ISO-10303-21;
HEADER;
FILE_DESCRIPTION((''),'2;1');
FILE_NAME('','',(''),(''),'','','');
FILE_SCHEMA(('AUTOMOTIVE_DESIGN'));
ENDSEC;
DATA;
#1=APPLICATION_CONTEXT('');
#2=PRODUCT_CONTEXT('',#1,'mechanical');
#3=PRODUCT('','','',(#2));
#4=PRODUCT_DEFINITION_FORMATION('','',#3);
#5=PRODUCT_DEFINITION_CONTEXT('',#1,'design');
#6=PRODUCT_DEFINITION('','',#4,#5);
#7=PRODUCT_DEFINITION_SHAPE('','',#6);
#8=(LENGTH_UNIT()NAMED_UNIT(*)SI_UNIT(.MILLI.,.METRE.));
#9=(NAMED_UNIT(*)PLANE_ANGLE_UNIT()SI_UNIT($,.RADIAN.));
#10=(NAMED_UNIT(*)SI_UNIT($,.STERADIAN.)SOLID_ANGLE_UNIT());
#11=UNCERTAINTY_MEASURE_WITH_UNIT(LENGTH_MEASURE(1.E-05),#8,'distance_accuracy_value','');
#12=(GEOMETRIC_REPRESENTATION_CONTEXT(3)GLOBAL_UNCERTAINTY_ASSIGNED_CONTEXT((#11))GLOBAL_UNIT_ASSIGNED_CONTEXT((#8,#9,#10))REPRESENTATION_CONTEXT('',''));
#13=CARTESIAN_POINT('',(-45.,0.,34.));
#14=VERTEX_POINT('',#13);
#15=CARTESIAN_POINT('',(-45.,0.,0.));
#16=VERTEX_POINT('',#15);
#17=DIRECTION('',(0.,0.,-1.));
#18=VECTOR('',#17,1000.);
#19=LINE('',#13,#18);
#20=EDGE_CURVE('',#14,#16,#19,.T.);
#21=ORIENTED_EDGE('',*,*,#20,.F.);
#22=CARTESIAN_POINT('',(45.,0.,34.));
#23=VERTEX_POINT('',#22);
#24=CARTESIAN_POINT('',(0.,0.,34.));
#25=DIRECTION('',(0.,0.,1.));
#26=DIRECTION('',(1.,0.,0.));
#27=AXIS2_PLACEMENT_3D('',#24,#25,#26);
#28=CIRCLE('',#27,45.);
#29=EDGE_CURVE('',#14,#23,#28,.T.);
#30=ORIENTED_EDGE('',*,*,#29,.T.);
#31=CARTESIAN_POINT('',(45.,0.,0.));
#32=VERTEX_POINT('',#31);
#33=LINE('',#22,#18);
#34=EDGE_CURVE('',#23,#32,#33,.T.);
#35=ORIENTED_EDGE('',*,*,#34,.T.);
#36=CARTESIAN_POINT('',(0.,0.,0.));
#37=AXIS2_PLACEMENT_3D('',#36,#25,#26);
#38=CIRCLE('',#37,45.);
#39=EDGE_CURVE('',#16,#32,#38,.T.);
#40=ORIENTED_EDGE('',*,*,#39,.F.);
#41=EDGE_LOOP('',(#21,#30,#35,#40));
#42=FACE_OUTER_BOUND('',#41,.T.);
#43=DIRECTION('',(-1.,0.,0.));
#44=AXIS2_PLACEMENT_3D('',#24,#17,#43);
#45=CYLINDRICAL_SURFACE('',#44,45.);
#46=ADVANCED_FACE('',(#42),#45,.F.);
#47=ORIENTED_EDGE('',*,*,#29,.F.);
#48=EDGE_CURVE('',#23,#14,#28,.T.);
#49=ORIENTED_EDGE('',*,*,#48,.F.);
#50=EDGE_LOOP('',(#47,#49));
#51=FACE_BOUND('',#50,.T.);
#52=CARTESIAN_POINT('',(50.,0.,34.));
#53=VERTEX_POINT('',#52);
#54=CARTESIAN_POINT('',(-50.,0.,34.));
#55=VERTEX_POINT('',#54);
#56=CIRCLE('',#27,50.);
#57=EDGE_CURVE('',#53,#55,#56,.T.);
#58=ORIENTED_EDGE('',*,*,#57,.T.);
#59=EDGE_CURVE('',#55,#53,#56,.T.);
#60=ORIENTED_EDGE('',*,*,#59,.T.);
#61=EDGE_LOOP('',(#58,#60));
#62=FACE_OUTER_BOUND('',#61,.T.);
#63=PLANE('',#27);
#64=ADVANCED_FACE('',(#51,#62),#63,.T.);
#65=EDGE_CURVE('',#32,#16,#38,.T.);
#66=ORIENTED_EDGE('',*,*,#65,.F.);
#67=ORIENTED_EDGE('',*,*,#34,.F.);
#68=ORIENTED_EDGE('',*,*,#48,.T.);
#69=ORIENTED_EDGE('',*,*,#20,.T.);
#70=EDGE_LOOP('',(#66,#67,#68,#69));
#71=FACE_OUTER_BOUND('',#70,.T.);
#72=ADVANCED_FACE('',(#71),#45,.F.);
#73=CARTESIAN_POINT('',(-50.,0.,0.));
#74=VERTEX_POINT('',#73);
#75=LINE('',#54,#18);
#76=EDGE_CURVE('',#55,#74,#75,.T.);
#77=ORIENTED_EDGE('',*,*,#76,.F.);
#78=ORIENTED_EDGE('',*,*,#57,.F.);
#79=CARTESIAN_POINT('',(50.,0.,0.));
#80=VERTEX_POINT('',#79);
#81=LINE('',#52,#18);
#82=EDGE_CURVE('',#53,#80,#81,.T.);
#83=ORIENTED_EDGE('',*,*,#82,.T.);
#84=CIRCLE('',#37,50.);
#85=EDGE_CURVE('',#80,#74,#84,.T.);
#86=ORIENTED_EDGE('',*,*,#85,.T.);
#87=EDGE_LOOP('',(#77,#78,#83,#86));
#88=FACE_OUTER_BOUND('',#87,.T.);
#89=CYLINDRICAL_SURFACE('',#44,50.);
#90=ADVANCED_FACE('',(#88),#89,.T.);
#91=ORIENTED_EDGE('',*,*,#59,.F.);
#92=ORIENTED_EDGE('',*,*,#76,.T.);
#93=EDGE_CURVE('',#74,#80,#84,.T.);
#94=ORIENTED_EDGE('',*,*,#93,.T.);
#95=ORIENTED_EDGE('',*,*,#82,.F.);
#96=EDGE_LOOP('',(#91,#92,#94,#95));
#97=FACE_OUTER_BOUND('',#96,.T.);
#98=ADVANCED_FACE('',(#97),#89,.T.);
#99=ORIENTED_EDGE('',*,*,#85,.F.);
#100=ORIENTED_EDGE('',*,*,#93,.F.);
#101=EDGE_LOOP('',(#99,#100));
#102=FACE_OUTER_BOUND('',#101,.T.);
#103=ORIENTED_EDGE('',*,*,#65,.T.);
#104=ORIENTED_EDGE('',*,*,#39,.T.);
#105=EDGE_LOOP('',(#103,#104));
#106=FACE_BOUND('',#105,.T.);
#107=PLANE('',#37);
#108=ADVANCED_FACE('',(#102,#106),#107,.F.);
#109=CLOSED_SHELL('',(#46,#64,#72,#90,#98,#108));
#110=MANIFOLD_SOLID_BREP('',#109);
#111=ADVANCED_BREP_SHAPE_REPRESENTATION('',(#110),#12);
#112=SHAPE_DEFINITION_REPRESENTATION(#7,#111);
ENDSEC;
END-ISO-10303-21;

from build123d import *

# Parameters (mm, degrees)
SKETCH_1_R      = 50
SKETCH_1_R_2    = 45
EXTRUDE_1_DEPTH = 34


with BuildPart() as part:
    # 草图1 → 凸台-拉伸1 (new body)
    with BuildSketch(Plane.XY):
        Circle(SKETCH_1_R)
        Circle(SKETCH_1_R_2, mode=Mode.SUBTRACT)
    extrude(amount=EXTRUDE_1_DEPTH)


solid = part.part
